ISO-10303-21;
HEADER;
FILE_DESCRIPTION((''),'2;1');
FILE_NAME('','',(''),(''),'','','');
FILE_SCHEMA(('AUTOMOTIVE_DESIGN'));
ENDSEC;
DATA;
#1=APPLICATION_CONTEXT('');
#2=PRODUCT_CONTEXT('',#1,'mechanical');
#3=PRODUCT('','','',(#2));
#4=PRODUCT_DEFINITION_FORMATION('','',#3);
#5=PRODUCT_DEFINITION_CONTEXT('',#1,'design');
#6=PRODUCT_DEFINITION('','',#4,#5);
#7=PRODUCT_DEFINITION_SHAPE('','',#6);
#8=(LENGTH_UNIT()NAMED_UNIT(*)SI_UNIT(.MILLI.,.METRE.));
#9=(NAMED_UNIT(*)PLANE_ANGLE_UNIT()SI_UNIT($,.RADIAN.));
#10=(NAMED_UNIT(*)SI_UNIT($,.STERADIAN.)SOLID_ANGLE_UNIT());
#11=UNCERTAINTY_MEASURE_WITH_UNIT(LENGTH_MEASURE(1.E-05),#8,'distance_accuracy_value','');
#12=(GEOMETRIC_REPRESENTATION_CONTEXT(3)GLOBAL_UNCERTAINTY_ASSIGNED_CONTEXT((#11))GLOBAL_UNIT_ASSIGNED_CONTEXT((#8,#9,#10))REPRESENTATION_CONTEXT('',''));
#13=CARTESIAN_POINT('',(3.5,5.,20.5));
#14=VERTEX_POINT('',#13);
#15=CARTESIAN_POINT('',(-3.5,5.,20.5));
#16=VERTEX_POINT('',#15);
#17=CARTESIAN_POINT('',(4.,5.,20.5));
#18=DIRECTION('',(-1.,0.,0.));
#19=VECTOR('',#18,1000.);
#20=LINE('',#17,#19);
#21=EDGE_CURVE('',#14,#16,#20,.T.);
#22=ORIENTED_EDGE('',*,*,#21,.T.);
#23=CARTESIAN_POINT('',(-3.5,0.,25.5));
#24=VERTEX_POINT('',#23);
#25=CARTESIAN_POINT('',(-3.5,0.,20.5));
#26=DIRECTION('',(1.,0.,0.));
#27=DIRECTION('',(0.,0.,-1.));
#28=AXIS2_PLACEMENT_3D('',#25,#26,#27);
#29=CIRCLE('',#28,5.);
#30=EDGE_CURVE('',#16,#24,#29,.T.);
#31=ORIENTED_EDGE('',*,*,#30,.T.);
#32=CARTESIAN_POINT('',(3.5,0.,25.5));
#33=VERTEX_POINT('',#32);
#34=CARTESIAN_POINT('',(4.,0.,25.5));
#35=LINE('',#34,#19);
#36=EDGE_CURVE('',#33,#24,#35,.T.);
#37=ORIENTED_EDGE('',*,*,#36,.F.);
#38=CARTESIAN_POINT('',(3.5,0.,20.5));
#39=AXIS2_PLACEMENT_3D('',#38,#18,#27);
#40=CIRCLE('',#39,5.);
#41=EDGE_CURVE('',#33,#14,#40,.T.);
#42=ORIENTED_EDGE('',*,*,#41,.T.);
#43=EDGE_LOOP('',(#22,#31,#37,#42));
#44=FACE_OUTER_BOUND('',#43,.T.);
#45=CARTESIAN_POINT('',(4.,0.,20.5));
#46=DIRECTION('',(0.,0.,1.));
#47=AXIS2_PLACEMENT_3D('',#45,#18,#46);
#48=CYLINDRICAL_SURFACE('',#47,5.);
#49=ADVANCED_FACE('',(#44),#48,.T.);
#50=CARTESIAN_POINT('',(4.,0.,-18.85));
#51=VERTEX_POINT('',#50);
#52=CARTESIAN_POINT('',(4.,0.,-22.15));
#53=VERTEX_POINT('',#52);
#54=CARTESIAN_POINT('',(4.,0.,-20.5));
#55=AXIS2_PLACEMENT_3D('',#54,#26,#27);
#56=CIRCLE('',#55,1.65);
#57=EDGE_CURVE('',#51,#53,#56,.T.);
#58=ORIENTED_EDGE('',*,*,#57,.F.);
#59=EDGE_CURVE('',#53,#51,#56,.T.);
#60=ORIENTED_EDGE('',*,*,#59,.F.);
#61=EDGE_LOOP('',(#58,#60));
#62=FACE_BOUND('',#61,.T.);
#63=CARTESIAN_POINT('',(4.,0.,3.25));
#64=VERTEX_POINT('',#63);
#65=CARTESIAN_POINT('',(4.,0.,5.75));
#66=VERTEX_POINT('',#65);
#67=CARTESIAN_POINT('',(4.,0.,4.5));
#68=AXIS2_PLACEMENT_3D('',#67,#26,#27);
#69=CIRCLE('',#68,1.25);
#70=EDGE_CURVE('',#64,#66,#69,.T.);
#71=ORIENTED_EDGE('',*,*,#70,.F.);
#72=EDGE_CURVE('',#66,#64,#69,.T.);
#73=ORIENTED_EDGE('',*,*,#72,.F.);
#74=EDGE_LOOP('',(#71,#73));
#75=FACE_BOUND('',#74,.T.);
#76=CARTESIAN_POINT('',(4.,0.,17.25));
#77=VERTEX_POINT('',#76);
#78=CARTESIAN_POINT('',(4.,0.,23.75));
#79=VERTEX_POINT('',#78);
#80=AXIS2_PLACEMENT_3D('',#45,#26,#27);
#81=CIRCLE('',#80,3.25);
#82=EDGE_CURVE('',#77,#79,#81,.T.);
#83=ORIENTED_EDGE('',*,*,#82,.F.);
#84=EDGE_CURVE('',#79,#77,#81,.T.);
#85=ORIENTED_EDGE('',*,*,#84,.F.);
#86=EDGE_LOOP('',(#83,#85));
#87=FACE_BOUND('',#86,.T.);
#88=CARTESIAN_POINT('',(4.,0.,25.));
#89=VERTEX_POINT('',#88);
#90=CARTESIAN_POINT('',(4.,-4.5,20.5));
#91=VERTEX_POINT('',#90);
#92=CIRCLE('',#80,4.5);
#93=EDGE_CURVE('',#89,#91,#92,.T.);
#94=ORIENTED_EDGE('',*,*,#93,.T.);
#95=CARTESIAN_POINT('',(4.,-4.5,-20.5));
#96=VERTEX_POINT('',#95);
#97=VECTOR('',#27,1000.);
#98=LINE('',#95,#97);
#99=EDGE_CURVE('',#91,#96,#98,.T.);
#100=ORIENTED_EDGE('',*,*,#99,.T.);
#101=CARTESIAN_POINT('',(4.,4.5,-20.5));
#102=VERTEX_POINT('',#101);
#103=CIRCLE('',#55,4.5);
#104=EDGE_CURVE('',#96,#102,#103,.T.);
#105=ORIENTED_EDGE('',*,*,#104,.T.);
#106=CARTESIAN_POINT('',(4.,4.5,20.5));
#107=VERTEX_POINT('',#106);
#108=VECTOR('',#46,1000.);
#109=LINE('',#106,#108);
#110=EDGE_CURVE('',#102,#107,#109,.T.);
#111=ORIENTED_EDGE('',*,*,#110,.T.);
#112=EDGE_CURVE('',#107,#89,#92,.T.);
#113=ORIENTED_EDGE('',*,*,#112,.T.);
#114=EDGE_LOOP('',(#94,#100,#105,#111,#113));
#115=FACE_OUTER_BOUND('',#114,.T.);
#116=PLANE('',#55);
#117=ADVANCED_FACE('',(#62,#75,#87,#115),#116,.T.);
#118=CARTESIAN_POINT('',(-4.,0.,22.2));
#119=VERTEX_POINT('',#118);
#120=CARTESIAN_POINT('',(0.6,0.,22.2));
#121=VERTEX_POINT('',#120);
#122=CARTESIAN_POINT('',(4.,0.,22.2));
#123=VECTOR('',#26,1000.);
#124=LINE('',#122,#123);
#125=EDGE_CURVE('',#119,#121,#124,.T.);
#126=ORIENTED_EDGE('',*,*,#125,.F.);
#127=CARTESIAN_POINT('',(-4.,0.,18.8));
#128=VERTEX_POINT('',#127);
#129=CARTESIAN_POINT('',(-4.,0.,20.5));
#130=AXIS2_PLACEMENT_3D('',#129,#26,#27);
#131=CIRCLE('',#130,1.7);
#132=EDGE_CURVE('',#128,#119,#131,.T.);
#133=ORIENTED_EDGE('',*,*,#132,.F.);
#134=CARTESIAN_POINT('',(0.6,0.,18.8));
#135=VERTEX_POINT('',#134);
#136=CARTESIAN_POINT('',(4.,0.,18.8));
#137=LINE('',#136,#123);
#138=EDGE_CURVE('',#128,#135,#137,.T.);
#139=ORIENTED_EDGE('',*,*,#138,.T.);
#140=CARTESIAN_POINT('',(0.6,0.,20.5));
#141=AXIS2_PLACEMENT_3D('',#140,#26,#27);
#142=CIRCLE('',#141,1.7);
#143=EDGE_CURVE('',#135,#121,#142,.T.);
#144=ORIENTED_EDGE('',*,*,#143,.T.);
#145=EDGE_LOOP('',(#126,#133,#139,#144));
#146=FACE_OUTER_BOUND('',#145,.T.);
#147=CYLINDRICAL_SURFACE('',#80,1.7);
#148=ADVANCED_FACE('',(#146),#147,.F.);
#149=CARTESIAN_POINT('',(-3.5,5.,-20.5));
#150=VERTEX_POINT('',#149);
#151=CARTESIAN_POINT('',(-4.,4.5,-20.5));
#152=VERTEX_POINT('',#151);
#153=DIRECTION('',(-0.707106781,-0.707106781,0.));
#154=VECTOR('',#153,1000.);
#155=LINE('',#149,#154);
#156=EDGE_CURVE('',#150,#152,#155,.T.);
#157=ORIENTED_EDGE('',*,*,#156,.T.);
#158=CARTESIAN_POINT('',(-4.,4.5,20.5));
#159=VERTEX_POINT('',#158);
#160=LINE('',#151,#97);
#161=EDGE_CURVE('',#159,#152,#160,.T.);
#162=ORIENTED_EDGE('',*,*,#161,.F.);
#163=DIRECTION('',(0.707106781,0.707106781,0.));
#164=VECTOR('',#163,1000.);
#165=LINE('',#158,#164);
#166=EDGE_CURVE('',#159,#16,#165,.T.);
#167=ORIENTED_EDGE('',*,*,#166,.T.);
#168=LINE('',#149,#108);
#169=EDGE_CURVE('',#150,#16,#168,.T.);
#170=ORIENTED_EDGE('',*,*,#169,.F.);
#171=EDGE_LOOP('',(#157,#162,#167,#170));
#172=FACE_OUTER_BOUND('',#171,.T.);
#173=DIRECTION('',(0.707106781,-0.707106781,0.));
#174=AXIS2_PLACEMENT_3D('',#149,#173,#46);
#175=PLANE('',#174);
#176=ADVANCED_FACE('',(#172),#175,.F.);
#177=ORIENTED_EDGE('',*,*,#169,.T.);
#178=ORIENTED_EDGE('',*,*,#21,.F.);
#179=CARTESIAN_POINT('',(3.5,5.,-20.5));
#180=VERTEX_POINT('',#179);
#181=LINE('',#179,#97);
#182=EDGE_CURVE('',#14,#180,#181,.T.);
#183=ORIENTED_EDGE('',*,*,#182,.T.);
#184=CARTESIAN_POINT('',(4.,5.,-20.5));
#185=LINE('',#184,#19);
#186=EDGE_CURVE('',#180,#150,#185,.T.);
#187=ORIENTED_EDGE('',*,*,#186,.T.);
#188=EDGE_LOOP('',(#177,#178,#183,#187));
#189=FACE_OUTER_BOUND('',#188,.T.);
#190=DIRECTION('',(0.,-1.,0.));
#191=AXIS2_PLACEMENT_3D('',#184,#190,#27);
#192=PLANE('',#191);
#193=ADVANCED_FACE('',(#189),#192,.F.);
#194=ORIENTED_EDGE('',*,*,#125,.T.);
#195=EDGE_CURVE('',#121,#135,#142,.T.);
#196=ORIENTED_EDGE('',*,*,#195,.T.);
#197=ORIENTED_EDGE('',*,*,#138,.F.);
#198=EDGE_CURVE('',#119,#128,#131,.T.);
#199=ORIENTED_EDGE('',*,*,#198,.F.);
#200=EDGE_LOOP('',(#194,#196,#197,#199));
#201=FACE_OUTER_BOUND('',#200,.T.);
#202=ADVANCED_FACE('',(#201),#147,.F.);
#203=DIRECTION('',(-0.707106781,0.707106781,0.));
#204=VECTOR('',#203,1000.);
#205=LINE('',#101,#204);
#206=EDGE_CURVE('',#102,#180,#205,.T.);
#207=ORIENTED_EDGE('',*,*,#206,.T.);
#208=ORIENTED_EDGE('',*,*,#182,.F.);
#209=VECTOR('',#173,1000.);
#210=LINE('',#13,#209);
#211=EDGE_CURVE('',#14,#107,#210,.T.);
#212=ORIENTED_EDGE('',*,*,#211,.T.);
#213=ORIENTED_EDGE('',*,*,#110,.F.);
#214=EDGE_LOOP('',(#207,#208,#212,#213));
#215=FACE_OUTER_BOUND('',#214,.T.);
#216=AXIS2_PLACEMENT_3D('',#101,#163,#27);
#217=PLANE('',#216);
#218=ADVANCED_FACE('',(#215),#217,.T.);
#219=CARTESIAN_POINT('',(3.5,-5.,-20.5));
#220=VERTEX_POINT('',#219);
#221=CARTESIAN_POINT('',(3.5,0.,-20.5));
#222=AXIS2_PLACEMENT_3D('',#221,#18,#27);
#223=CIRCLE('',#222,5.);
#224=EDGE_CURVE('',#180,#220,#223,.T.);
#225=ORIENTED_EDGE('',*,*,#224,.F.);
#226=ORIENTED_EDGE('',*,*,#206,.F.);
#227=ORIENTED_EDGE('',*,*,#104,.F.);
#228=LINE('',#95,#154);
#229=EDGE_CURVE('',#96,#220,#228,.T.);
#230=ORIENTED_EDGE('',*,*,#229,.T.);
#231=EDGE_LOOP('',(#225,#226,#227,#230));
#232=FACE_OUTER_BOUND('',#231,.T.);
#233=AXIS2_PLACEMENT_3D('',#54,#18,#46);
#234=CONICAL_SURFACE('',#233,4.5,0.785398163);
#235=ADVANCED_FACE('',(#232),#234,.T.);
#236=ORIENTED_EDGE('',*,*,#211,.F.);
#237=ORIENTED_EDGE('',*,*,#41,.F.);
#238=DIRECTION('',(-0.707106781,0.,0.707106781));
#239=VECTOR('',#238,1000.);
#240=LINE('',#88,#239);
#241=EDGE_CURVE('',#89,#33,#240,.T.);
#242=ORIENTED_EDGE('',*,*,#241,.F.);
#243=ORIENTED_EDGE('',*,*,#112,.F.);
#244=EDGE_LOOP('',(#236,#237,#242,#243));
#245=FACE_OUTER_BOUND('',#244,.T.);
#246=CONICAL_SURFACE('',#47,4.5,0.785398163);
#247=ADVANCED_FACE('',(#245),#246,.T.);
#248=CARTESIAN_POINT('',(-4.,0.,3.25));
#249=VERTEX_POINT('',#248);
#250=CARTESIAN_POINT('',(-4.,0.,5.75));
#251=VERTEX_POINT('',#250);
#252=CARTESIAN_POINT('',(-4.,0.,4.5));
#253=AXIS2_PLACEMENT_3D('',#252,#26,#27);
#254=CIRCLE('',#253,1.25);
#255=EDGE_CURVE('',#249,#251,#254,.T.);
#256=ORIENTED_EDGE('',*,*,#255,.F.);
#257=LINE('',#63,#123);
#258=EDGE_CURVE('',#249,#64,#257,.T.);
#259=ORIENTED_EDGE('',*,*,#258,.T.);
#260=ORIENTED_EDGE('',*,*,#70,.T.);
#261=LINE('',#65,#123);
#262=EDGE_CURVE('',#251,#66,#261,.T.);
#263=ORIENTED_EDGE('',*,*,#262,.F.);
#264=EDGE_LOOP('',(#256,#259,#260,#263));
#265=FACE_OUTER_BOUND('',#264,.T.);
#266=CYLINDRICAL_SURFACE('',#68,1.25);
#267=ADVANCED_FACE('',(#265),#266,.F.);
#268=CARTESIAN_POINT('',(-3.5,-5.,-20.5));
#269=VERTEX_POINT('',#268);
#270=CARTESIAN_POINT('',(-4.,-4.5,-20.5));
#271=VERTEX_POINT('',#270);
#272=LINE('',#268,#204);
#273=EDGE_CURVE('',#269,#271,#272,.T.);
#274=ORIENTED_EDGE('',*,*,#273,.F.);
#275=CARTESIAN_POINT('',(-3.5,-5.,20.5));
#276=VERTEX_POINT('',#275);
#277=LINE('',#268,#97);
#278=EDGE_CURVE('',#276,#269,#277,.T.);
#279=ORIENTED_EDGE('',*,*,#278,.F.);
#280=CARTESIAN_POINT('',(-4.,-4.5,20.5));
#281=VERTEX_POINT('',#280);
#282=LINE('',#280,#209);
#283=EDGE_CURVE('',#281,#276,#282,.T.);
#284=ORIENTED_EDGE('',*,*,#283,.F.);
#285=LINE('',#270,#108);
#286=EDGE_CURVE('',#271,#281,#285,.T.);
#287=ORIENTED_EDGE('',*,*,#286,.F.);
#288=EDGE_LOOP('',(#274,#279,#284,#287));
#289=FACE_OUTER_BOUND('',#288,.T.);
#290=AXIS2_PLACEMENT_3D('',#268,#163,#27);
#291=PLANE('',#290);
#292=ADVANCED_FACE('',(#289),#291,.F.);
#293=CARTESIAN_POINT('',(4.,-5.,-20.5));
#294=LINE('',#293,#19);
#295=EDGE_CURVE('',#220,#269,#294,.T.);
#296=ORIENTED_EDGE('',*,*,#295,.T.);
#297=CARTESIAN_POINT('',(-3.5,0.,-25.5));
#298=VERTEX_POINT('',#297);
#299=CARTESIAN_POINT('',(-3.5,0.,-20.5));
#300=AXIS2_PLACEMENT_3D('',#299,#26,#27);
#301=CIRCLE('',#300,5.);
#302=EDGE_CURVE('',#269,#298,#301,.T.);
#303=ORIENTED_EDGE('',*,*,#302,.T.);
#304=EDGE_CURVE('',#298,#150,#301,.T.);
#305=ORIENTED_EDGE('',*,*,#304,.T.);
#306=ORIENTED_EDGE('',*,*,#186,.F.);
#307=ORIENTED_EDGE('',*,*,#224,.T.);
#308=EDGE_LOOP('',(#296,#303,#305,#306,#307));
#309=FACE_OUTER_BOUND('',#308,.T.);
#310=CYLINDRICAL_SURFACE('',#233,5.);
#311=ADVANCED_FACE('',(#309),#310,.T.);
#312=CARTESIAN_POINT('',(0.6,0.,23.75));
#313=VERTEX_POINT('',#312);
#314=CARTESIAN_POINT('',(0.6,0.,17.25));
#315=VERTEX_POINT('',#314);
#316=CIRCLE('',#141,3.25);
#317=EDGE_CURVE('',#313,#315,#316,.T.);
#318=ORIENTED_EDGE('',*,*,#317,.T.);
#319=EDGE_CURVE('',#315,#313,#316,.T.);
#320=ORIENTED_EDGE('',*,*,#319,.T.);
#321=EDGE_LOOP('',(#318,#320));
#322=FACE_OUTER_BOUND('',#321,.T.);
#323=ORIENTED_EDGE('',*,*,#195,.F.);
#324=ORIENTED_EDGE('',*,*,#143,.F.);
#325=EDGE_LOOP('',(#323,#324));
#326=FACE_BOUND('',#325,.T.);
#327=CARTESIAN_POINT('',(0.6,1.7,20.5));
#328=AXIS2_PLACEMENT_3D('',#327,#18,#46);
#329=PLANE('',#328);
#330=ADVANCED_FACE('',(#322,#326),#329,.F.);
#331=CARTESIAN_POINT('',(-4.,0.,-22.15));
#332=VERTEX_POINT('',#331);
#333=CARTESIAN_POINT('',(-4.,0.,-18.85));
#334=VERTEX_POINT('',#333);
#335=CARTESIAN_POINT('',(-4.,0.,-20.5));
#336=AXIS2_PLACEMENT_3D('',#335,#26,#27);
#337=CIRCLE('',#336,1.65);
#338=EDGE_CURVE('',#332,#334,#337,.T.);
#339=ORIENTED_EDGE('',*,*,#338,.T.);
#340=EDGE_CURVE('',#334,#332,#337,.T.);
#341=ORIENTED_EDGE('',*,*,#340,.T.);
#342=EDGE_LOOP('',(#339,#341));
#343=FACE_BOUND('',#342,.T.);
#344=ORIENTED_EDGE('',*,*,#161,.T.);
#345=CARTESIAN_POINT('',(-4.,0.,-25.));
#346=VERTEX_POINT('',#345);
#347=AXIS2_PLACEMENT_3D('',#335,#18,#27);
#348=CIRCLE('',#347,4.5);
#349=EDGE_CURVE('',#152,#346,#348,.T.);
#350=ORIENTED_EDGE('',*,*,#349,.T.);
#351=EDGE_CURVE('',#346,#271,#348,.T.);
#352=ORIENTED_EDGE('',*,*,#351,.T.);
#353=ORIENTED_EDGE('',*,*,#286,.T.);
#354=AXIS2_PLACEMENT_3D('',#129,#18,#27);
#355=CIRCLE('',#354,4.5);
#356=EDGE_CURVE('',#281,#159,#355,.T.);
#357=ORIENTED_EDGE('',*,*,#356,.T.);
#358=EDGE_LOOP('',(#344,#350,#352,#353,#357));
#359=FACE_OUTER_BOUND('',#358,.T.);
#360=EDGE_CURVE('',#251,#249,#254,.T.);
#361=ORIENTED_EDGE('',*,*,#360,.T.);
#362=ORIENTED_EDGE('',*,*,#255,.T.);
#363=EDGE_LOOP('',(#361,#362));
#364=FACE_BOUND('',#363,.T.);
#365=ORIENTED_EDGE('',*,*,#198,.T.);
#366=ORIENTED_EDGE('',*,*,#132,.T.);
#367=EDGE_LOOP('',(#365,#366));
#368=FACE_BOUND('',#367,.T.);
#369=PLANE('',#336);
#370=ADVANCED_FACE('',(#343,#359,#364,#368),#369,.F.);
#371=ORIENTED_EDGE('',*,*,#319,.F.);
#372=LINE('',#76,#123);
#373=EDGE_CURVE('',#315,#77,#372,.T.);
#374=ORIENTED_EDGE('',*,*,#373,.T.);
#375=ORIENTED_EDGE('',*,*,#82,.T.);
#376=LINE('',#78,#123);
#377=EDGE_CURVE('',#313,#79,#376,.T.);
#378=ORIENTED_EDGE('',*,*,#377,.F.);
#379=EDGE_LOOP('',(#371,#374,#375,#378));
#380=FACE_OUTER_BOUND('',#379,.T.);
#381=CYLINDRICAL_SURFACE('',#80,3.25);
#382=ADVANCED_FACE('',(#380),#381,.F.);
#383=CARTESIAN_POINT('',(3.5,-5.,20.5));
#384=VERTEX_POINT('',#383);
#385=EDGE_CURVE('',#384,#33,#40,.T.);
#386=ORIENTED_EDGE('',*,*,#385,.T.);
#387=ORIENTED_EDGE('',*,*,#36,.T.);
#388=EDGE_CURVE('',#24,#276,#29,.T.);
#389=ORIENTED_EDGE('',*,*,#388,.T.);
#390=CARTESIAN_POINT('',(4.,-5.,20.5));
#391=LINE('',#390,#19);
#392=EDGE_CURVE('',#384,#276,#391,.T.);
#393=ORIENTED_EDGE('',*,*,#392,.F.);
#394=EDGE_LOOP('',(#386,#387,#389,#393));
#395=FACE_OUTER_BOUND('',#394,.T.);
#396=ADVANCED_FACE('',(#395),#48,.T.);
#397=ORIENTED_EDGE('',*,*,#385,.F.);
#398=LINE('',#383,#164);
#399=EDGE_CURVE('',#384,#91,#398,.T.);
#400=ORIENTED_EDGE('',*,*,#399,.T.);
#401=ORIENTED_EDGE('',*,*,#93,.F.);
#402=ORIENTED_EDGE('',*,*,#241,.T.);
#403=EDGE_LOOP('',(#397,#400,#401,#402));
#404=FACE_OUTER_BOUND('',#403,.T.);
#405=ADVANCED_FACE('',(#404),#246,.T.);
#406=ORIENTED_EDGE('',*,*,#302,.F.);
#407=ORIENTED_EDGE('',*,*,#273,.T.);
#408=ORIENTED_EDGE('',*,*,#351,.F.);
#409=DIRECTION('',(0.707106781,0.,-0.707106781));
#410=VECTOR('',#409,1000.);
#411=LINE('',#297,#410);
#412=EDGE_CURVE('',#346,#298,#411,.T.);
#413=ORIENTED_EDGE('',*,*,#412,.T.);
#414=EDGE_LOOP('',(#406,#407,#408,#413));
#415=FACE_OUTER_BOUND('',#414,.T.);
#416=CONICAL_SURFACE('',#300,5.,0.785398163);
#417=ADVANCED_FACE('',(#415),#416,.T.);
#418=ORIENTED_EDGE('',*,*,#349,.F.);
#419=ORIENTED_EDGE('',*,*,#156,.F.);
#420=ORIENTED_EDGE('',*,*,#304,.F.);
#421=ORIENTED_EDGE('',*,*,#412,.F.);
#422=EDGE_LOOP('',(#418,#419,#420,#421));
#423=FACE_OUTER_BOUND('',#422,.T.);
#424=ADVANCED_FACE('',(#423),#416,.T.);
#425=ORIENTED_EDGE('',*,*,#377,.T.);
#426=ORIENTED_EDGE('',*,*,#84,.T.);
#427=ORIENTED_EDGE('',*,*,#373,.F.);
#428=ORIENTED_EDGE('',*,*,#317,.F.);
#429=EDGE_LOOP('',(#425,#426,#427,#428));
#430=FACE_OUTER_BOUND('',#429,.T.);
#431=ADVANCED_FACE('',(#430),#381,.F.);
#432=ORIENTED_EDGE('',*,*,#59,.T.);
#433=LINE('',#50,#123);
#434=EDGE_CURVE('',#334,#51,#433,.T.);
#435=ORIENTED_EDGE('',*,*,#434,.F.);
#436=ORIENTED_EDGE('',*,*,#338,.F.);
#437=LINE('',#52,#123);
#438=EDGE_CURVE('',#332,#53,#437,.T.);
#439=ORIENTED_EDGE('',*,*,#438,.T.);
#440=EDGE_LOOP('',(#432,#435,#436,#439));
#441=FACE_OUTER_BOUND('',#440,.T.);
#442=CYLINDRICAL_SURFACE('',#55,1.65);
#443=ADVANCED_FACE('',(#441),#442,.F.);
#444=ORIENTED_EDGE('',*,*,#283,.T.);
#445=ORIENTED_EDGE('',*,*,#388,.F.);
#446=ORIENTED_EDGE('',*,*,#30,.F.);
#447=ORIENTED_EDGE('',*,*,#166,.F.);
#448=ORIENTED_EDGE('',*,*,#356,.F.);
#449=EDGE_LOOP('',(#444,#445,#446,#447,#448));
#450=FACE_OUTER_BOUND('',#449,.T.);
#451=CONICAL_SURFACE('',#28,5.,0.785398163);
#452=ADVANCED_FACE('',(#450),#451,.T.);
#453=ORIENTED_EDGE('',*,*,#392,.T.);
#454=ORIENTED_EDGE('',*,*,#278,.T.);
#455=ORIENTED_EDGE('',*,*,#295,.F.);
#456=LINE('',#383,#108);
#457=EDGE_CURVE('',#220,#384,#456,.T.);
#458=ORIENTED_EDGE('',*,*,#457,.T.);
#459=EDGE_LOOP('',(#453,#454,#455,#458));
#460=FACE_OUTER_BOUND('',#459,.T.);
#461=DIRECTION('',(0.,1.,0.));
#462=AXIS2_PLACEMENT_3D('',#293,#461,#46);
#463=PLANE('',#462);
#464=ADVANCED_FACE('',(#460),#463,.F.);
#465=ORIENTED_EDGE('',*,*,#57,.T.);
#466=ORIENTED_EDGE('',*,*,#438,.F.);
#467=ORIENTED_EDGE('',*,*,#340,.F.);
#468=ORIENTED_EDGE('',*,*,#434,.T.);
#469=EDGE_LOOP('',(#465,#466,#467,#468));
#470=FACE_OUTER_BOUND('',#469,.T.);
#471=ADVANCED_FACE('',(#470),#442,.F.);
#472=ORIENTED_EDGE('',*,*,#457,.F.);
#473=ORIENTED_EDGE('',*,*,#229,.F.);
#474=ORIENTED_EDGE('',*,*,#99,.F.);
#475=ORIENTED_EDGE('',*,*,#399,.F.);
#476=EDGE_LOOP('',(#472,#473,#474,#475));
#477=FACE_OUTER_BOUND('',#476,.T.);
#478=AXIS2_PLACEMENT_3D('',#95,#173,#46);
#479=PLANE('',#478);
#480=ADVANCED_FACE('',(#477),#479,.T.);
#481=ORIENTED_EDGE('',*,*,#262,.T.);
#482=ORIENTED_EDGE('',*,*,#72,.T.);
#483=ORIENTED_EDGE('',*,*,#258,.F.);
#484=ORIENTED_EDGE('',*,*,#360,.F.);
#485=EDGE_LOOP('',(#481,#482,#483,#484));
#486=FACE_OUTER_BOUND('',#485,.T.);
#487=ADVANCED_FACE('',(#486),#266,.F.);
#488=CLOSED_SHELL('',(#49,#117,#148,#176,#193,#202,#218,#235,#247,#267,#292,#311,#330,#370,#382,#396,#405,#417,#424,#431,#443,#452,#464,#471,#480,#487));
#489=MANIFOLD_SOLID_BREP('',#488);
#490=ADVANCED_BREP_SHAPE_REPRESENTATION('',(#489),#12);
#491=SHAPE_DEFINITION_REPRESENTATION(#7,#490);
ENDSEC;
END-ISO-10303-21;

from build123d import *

# Parameters (mm, degrees)
EXTRUDE_1_DEPTH           = 4
HOLE_WIZARD_1_D           = 3.4
HOLE_WIZARD_1_CBORE_D     = 6.5
HOLE_WIZARD_1_CBORE_DEPTH = 3.4
HOLE_WIZARD_M3_1_D        = 2.5
HOLE_WIZARD_M4_1_D        = 3.3
CHAMFER_1_SIZE            = 0.5


with BuildPart() as part:
    # 草图1 → 凸台-拉伸1 (new, symmetric)
    with BuildSketch(Plane(origin=(0, 0, 0), x_dir=(0, 0, -1), z_dir=(1, 0, 0))):
        with BuildLine():
            Line((20.5, -5), (-20.5, -5))
            ThreePointArc((-20.5, -5), (-25.5, 0), (-20.5, 5))
            Line((-20.5, 5), (20.5, 5))
            ThreePointArc((20.5, 5), (25.5, 0), (20.5, -5))
        make_face()
    extrude(amount=EXTRUDE_1_DEPTH, both=True)

    # 打孔尺寸(%根据)内六角圆柱头螺钉的类型1 (through all)
    with Locations(Plane(origin=(4, 0, 0), x_dir=(0, 0, -1), z_dir=(1, 0, 0))):
        with Locations((-20.5, 0)):
            CounterBoreHole(HOLE_WIZARD_1_D / 2, HOLE_WIZARD_1_CBORE_D / 2, HOLE_WIZARD_1_CBORE_DEPTH)

    # M3 螺纹孔1 (through all)
    with Locations(Plane(origin=(4, 0, 0), x_dir=(0, 0, -1), z_dir=(1, 0, 0))):
        with Locations((-4.5, 0)):
            Hole(HOLE_WIZARD_M3_1_D / 2)

    # M4 螺纹孔1 (through all)
    with Locations(Plane(origin=(4, 0, 0), x_dir=(0, 0, -1), z_dir=(1, 0, 0))):
        with Locations((20.5, 0)):
            Hole(HOLE_WIZARD_M4_1_D / 2)

    # 倒角1
    chamfer_1_edges = [part.edges().sort_by_distance(p)[0] for p in [
        (4, 0, 25.5),
        (4, -5, 0),
        (4, 0, -25.5),
        (-4, -5, 0),
        (-4, 0, 25.5),
        (-4, 5, 0),
        (-4, 0, -25.5),
        (4, 5, 0),
    ]]
    chamfer(chamfer_1_edges, length=CHAMFER_1_SIZE)


solid = part.part
